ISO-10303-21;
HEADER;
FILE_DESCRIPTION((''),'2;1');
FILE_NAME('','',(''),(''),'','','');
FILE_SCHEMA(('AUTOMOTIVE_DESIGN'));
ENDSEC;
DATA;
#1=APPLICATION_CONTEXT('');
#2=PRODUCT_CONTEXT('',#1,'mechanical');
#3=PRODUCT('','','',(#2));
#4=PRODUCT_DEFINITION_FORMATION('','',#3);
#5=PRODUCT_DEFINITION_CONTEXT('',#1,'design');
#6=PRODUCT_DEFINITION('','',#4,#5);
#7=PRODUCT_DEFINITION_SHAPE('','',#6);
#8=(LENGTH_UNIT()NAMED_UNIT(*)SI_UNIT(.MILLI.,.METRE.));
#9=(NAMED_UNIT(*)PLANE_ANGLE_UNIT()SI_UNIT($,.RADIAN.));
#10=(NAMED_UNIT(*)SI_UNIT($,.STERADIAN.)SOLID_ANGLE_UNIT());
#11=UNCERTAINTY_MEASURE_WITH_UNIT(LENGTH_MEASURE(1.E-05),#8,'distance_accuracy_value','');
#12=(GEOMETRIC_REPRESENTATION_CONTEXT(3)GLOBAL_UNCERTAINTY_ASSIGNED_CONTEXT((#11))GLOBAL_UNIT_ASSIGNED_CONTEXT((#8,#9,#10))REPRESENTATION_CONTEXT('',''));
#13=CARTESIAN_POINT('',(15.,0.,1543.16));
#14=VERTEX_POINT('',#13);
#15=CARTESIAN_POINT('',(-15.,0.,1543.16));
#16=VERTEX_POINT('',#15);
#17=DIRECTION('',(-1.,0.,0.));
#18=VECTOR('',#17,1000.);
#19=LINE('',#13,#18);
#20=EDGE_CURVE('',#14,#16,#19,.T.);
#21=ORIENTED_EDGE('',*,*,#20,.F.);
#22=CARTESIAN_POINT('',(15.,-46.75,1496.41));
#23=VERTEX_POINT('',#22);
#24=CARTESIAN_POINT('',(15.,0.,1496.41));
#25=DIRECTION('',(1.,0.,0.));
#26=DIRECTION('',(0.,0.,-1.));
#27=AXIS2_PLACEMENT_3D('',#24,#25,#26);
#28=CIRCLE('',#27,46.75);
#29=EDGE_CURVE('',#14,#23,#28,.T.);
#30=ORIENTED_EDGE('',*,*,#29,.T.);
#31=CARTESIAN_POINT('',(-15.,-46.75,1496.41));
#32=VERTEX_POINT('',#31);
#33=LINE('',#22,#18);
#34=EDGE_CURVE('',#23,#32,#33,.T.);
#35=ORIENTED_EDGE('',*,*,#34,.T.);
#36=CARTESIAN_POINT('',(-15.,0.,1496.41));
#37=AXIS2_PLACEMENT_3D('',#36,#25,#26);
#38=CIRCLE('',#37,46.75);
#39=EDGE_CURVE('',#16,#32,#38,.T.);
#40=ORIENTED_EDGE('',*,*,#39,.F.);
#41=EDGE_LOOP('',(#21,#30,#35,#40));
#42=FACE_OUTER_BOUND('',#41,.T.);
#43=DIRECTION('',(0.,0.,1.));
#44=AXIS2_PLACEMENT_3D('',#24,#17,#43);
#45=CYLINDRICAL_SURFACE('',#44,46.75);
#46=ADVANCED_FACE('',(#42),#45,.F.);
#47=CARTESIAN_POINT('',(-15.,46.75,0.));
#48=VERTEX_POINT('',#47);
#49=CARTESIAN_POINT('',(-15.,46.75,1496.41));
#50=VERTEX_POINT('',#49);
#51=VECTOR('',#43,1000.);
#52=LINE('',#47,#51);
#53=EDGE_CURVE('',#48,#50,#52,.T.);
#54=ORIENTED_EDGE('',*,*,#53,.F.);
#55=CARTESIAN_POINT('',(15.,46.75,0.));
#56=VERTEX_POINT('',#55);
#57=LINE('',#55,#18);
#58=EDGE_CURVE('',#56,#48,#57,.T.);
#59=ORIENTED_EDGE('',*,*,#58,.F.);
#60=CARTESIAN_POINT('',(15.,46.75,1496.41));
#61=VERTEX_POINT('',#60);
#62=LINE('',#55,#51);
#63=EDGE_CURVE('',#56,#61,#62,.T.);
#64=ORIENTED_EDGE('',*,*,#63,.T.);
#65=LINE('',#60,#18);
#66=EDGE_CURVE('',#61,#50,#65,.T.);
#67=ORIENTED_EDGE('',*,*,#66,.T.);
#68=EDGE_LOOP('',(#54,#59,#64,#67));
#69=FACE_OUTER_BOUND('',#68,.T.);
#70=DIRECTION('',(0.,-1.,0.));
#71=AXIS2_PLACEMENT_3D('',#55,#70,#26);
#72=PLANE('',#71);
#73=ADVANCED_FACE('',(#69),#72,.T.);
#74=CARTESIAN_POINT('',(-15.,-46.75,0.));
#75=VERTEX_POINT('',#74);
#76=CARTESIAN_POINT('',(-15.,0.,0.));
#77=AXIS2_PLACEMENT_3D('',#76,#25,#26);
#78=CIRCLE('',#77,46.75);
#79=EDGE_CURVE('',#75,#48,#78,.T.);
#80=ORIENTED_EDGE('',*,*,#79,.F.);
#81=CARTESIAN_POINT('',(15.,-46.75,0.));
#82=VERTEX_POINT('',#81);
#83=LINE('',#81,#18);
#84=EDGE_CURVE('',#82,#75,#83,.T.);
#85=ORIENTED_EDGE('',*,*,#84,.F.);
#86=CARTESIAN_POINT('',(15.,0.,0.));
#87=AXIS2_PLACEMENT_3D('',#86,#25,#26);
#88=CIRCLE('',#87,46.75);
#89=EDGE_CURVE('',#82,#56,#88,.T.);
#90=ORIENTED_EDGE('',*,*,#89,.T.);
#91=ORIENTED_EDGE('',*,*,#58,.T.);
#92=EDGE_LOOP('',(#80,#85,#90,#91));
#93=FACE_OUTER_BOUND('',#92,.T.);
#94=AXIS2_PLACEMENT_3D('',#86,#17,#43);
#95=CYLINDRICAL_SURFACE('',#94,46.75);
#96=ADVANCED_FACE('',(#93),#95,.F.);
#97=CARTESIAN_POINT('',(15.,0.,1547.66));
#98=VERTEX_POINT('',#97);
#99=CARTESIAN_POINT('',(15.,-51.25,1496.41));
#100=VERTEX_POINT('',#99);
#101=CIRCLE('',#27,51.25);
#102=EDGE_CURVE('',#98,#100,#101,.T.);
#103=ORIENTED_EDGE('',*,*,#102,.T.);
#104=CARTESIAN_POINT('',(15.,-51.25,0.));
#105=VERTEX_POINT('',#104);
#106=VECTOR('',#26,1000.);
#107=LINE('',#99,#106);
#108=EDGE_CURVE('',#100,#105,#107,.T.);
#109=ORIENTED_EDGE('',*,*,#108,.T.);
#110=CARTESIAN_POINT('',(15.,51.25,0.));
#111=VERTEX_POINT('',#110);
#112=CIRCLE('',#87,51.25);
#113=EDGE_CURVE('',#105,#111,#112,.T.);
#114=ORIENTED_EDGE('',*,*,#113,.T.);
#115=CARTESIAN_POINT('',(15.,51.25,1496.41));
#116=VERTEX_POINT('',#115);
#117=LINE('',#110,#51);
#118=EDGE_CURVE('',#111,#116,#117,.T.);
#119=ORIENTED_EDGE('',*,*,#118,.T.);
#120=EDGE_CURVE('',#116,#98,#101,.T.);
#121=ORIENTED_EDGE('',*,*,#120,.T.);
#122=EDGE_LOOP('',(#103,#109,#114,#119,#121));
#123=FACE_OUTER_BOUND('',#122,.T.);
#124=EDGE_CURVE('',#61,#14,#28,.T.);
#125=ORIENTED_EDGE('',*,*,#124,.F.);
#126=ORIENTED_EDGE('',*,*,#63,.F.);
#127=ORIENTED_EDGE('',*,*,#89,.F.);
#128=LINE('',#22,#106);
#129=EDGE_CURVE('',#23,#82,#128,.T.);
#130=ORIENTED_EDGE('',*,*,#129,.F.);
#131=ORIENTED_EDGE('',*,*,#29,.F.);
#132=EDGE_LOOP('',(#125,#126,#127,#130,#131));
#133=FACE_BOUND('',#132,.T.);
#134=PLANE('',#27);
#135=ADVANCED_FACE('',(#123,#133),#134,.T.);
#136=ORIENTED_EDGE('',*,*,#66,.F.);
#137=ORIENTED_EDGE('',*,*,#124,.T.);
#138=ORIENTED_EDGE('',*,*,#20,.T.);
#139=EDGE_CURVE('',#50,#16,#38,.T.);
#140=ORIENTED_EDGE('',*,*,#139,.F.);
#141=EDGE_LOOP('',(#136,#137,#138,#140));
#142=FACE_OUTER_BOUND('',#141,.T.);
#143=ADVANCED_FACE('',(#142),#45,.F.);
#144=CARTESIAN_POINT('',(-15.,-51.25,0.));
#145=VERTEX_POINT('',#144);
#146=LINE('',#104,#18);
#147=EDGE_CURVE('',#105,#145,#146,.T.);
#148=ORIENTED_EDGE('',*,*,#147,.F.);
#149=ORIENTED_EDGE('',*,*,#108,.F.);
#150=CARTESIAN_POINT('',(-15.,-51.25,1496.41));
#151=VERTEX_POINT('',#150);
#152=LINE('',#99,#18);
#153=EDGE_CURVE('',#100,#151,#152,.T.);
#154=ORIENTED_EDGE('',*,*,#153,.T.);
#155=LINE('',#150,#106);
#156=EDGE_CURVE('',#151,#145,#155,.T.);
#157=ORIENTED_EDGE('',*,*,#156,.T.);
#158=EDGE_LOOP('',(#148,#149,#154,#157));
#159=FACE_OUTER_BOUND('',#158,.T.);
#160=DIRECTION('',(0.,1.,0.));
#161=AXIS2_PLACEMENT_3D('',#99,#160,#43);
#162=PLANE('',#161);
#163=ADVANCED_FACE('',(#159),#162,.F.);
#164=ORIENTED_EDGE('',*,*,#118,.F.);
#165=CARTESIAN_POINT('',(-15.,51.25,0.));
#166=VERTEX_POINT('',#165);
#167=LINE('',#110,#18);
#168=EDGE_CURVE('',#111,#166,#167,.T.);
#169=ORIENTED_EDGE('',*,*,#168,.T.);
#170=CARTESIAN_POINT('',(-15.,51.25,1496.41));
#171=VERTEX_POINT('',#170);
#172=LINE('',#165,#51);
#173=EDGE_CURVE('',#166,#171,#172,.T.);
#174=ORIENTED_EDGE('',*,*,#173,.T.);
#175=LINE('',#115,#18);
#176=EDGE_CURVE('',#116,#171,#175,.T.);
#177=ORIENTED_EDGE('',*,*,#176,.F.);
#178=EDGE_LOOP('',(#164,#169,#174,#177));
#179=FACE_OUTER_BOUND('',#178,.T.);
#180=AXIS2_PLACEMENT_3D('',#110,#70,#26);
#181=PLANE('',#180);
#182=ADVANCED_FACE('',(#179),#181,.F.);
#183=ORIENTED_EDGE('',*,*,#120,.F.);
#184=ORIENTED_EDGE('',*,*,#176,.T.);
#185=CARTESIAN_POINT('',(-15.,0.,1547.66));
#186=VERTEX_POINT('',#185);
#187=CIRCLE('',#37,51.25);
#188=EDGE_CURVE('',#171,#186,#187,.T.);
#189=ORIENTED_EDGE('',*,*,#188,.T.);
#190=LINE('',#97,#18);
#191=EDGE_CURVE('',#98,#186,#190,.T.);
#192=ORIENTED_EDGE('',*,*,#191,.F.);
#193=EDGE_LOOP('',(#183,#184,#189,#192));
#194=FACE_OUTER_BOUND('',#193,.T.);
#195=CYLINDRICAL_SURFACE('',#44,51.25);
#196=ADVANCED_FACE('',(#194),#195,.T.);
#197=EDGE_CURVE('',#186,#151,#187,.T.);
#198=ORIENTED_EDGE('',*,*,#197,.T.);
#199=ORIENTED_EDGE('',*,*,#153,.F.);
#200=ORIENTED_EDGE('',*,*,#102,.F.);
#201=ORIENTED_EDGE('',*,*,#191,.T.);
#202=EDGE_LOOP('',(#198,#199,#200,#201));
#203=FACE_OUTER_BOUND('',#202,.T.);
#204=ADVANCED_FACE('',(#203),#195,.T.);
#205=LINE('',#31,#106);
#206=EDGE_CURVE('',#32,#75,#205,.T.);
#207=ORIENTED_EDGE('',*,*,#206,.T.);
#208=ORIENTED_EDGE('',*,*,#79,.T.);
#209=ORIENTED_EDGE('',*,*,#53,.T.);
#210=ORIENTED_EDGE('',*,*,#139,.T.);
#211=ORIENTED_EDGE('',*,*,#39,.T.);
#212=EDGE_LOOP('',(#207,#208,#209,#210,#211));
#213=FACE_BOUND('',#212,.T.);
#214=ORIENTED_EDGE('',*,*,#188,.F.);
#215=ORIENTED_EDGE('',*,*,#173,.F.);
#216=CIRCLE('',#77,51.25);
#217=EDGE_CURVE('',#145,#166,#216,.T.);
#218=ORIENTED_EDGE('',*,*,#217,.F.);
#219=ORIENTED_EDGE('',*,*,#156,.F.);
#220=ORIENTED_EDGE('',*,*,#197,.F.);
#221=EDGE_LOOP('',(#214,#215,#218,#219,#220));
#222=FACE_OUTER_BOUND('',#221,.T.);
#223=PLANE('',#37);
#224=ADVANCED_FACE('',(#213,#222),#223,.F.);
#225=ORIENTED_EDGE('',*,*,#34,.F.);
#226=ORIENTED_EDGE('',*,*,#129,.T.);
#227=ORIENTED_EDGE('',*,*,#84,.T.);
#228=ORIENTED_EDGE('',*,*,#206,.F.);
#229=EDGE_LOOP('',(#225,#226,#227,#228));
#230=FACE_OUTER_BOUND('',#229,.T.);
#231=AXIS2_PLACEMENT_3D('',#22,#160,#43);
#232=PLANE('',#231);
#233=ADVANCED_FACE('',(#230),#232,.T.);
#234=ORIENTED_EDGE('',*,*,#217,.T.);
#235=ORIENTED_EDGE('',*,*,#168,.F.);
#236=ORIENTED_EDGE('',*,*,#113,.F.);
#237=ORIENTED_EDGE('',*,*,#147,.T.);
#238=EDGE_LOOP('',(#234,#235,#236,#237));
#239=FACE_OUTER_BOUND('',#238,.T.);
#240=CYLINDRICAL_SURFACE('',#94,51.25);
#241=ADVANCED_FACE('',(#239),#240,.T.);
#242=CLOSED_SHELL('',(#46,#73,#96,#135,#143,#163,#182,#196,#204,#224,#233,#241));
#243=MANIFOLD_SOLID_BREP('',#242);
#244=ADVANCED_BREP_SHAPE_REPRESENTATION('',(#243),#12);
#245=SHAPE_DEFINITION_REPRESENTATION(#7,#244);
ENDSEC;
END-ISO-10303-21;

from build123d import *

# Parameters (mm, degrees)
EXTRUDE_1_DEPTH = 15


with BuildPart() as part:
    # 草图2 → 拉伸-薄壁1 (new, symmetric)
    with BuildSketch(Plane(origin=(0, 0, 0), x_dir=(0, 0, -1), z_dir=(1, 0, 0))):
        with BuildLine():
            Line((-1496.41, -51.25), (0, -51.25))
            ThreePointArc((0, -51.25), (51.25, 0), (0, 51.25))
            Line((0, 51.25), (-1496.41, 51.25))
            ThreePointArc((-1496.41, 51.25), (-1547.66, 0), (-1496.41, -51.25))
        make_face()
        with BuildLine():
            Line((-1496.41, -46.75), (0, -46.75))
            ThreePointArc((0, -46.75), (46.75, 0), (0, 46.75))
            Line((0, 46.75), (-1496.41, 46.75))
            ThreePointArc((-1496.41, 46.75), (-1543.16, 0), (-1496.41, -46.75))
        make_face(mode=Mode.SUBTRACT)
    extrude(amount=EXTRUDE_1_DEPTH, both=True)


solid = part.part
